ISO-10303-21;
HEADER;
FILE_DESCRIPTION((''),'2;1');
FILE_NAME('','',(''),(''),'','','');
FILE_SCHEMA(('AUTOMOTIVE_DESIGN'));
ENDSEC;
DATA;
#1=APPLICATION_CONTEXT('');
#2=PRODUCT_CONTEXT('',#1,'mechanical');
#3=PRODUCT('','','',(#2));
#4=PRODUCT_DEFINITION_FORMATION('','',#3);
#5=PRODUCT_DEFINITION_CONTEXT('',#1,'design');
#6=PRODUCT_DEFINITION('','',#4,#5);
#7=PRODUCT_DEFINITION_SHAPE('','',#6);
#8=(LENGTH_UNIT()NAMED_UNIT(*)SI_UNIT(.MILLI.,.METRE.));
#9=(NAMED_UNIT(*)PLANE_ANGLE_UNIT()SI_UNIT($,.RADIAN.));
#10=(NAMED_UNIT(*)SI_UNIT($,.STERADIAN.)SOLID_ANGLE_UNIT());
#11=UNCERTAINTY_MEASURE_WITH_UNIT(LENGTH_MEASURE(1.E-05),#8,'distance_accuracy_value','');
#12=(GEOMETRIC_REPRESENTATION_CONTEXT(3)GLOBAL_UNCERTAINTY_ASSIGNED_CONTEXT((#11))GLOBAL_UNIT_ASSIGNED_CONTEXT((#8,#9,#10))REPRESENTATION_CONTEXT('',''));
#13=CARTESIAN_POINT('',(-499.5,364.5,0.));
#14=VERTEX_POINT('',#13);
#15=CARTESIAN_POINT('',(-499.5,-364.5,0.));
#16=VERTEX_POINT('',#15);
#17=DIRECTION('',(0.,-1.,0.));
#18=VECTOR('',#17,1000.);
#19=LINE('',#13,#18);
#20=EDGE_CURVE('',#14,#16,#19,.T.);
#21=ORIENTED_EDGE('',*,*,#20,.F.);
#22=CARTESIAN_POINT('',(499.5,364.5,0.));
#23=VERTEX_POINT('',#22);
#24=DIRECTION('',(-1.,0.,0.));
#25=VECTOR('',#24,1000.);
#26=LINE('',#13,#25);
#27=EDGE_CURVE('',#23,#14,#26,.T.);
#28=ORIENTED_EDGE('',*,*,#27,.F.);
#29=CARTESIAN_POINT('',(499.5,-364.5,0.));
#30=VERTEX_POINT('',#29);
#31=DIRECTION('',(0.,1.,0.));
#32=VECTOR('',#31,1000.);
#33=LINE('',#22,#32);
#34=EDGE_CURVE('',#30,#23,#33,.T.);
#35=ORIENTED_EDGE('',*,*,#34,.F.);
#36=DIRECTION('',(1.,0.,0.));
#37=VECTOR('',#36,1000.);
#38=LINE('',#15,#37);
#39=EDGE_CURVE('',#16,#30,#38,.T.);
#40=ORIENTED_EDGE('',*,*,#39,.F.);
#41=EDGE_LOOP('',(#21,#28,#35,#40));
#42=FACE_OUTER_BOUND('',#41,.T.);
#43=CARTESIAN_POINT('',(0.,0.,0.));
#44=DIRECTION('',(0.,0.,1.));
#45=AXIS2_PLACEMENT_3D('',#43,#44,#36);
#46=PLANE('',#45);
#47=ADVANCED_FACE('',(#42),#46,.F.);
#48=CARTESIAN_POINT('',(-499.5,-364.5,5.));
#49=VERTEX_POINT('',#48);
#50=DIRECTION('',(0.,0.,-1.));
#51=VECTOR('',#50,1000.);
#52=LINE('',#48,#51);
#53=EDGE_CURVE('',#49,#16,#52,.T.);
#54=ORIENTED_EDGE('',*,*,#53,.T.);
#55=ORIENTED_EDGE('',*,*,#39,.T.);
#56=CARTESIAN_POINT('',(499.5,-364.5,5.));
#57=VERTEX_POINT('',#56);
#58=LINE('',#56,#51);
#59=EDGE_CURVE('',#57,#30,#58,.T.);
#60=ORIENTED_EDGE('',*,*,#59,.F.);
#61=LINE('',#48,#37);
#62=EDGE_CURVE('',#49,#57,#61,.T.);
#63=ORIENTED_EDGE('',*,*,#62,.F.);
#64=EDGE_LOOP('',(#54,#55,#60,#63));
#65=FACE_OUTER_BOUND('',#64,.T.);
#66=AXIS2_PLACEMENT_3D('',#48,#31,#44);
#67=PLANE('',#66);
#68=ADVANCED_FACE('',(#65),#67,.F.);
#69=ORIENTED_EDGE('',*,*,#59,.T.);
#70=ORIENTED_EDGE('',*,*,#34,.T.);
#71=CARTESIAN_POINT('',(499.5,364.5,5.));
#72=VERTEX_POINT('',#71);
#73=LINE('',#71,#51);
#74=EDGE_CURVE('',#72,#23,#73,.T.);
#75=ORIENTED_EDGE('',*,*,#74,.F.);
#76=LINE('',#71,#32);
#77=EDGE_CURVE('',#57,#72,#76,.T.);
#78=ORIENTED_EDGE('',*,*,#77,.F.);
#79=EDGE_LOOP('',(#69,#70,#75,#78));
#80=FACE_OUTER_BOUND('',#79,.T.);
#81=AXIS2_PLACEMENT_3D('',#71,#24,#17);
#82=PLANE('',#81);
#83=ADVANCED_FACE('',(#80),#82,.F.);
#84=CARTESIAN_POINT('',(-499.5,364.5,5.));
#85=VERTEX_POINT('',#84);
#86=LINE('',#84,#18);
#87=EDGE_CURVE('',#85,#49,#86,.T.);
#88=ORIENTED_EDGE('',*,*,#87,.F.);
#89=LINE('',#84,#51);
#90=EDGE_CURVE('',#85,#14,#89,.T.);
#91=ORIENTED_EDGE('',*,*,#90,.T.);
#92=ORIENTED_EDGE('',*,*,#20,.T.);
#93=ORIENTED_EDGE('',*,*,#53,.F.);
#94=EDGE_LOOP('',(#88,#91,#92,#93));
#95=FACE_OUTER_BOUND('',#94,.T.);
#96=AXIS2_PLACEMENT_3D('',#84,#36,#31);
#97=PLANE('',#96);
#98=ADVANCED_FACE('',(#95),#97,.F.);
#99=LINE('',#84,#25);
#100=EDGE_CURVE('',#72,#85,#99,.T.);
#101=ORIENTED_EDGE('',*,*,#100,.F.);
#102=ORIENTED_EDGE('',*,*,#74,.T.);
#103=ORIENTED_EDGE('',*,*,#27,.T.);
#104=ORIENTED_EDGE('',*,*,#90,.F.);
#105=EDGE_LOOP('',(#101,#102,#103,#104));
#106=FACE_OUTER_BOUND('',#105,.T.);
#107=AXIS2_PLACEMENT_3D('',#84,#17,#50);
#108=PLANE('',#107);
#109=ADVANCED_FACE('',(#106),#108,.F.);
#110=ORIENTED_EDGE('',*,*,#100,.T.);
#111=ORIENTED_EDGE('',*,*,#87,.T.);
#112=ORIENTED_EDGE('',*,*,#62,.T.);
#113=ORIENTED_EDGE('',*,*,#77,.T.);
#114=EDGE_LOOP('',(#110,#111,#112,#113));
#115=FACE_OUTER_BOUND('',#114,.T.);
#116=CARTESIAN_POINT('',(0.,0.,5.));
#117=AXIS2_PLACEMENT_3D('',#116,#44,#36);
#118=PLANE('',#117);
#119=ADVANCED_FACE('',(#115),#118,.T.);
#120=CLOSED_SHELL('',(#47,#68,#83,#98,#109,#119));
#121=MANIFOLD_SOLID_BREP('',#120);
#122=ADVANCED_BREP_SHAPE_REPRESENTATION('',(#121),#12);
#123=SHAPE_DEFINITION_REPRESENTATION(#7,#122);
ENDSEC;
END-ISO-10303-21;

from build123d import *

# Parameters (mm, degrees)
SKETCH_1_W      = 999
SKETCH_1_H      = 729
EXTRUDE_1_DEPTH = 5


with BuildPart() as part:
    # 草图1 → 凸台-拉伸1 (new body)
    with BuildSketch(Plane.XY):
        Rectangle(SKETCH_1_W, SKETCH_1_H)
    extrude(amount=EXTRUDE_1_DEPTH)


solid = part.part
